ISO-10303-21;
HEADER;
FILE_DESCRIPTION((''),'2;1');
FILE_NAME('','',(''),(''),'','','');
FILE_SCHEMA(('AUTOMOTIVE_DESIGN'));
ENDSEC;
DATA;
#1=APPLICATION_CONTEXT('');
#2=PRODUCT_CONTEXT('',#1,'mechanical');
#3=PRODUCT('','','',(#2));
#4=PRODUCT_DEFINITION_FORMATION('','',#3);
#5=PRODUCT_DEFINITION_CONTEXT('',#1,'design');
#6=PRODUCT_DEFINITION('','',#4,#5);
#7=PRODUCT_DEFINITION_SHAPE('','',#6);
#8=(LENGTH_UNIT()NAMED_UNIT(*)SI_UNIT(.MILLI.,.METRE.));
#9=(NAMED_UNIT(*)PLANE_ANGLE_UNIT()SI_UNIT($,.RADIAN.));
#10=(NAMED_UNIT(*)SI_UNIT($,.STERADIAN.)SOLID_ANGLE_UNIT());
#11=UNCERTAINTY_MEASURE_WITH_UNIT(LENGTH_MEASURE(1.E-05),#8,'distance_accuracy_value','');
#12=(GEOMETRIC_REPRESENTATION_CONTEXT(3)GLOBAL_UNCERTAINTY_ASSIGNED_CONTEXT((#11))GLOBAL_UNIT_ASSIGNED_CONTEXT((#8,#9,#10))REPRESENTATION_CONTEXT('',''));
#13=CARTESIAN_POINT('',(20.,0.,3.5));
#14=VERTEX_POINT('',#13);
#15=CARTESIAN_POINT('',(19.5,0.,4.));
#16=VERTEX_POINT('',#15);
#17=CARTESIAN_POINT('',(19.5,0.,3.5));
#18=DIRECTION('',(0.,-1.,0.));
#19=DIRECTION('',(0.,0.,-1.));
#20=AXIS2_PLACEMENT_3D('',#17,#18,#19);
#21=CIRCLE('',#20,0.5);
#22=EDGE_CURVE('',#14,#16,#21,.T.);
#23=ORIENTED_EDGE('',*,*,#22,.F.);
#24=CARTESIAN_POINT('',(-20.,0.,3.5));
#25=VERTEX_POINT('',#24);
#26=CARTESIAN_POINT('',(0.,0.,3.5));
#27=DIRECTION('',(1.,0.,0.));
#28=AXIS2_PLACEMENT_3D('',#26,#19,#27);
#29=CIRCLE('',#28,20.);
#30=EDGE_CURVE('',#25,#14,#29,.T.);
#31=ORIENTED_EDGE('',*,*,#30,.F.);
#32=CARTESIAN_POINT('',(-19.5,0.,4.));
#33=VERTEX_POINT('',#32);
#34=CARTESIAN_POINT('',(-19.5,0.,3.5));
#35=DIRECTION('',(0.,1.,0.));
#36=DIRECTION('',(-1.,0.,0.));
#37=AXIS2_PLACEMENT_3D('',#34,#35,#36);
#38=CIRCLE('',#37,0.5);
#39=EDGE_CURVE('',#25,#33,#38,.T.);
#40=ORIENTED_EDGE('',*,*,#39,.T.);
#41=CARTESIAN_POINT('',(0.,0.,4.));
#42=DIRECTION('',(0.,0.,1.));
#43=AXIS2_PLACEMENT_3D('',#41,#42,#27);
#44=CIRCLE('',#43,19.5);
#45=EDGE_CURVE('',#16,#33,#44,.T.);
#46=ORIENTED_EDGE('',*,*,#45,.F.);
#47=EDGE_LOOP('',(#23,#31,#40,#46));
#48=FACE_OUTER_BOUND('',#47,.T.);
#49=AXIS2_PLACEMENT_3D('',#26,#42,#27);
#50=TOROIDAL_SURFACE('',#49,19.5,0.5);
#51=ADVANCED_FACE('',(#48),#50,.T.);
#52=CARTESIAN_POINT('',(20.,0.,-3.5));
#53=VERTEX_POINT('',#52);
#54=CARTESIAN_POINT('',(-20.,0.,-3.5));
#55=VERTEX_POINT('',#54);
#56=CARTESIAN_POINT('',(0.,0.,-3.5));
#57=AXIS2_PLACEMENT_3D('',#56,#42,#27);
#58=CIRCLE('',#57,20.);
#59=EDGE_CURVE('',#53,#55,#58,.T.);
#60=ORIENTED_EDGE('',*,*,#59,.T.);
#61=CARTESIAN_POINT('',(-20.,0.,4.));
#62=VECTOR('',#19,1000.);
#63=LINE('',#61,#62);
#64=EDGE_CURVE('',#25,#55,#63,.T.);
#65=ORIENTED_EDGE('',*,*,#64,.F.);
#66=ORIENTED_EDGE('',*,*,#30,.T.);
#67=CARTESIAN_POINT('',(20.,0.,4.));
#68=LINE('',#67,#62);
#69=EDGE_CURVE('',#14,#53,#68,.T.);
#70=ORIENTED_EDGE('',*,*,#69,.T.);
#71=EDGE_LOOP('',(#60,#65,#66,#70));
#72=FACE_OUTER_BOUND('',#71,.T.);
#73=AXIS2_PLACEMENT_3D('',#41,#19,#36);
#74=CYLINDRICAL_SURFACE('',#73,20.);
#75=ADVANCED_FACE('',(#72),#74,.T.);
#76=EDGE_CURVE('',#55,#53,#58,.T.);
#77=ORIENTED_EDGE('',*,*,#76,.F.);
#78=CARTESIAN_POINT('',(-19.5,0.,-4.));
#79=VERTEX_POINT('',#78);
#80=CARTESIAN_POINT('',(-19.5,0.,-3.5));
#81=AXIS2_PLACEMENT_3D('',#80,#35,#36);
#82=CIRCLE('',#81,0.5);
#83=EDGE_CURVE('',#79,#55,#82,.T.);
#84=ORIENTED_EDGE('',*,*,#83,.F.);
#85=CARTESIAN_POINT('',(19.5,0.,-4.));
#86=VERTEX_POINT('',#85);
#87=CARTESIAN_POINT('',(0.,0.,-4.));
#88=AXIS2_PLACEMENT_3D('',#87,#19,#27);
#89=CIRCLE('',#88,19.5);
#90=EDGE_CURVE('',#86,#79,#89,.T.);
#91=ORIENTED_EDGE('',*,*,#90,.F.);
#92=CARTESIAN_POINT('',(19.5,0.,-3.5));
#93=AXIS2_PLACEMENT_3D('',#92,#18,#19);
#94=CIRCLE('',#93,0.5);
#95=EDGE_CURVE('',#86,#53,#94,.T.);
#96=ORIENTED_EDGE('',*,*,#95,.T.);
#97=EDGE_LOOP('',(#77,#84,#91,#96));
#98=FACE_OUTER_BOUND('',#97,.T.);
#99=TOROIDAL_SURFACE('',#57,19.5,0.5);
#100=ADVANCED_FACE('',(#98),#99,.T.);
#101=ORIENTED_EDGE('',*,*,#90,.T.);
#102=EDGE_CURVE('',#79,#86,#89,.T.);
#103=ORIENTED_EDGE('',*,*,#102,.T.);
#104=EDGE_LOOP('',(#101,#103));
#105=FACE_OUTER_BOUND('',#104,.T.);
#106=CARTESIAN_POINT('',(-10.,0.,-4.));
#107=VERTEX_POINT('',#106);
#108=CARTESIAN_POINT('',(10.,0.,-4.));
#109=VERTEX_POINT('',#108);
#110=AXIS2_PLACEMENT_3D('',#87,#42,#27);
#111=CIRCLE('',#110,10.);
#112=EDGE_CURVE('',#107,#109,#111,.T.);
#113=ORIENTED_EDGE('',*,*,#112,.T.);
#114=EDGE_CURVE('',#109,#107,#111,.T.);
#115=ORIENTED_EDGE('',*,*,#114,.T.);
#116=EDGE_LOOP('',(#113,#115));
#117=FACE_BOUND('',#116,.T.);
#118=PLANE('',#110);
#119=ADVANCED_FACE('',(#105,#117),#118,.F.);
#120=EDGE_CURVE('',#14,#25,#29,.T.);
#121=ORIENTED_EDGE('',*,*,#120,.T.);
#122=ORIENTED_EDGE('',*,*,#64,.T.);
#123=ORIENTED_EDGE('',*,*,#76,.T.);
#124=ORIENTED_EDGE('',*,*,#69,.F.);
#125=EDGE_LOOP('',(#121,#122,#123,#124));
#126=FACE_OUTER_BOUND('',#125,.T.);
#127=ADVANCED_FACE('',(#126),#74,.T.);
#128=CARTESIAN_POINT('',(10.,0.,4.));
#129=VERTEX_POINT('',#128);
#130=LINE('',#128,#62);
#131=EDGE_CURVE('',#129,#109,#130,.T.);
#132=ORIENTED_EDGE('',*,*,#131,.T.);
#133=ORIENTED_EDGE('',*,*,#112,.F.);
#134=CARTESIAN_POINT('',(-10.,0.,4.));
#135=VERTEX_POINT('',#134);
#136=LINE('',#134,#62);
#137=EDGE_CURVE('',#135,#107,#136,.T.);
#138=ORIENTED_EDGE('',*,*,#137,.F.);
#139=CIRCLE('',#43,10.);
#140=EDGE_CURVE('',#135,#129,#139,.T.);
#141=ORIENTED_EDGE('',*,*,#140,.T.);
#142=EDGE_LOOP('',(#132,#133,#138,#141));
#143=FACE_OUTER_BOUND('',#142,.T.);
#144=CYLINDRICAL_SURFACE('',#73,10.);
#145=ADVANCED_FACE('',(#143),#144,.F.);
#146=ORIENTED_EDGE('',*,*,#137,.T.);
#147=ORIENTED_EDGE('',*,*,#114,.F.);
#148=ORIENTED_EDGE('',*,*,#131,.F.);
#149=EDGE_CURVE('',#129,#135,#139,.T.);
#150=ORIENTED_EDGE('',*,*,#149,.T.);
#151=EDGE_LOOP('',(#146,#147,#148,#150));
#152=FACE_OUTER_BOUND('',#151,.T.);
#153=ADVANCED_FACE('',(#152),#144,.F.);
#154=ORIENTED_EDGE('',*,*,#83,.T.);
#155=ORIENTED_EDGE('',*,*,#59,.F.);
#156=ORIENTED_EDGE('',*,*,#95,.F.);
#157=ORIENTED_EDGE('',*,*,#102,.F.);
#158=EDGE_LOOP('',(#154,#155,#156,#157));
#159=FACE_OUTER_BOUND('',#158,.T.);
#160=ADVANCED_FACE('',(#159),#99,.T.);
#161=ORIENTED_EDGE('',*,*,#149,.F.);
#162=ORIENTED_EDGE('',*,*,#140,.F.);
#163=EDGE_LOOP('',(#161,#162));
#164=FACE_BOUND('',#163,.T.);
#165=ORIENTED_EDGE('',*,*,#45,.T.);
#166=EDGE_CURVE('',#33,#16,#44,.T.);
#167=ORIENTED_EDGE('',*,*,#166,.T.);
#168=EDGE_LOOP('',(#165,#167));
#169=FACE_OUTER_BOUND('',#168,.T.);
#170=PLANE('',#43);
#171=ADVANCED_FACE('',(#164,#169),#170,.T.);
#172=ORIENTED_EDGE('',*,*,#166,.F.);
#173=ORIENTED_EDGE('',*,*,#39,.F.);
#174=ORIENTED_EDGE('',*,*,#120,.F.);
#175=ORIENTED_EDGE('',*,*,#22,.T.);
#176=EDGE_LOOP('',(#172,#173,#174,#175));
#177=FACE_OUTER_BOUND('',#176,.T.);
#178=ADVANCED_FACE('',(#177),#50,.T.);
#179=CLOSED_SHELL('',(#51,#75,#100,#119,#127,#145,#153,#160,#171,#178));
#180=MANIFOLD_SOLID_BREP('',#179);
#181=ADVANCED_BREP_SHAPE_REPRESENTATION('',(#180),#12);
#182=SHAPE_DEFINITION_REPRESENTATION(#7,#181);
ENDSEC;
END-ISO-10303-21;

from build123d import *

# Parameters (mm, degrees)
SKETCH_1_R      = 20
SKETCH_1_R_2    = 10
EXTRUDE_1_DEPTH = 4
FILLET_1_R      = 0.5


with BuildPart() as part:
    # 草图1 → 凸台-拉伸1 (new, symmetric)
    with BuildSketch(Plane.XY):
        Circle(SKETCH_1_R)
        Circle(SKETCH_1_R_2, mode=Mode.SUBTRACT)
    extrude(amount=EXTRUDE_1_DEPTH, both=True)

    # 圆角1
    fillet_1_edges = [part.edges().sort_by_distance(p)[0] for p in [
        (-20, 0, -4),
        (-20, 0, 4),
    ]]
    fillet(fillet_1_edges, radius=FILLET_1_R)


solid = part.part
